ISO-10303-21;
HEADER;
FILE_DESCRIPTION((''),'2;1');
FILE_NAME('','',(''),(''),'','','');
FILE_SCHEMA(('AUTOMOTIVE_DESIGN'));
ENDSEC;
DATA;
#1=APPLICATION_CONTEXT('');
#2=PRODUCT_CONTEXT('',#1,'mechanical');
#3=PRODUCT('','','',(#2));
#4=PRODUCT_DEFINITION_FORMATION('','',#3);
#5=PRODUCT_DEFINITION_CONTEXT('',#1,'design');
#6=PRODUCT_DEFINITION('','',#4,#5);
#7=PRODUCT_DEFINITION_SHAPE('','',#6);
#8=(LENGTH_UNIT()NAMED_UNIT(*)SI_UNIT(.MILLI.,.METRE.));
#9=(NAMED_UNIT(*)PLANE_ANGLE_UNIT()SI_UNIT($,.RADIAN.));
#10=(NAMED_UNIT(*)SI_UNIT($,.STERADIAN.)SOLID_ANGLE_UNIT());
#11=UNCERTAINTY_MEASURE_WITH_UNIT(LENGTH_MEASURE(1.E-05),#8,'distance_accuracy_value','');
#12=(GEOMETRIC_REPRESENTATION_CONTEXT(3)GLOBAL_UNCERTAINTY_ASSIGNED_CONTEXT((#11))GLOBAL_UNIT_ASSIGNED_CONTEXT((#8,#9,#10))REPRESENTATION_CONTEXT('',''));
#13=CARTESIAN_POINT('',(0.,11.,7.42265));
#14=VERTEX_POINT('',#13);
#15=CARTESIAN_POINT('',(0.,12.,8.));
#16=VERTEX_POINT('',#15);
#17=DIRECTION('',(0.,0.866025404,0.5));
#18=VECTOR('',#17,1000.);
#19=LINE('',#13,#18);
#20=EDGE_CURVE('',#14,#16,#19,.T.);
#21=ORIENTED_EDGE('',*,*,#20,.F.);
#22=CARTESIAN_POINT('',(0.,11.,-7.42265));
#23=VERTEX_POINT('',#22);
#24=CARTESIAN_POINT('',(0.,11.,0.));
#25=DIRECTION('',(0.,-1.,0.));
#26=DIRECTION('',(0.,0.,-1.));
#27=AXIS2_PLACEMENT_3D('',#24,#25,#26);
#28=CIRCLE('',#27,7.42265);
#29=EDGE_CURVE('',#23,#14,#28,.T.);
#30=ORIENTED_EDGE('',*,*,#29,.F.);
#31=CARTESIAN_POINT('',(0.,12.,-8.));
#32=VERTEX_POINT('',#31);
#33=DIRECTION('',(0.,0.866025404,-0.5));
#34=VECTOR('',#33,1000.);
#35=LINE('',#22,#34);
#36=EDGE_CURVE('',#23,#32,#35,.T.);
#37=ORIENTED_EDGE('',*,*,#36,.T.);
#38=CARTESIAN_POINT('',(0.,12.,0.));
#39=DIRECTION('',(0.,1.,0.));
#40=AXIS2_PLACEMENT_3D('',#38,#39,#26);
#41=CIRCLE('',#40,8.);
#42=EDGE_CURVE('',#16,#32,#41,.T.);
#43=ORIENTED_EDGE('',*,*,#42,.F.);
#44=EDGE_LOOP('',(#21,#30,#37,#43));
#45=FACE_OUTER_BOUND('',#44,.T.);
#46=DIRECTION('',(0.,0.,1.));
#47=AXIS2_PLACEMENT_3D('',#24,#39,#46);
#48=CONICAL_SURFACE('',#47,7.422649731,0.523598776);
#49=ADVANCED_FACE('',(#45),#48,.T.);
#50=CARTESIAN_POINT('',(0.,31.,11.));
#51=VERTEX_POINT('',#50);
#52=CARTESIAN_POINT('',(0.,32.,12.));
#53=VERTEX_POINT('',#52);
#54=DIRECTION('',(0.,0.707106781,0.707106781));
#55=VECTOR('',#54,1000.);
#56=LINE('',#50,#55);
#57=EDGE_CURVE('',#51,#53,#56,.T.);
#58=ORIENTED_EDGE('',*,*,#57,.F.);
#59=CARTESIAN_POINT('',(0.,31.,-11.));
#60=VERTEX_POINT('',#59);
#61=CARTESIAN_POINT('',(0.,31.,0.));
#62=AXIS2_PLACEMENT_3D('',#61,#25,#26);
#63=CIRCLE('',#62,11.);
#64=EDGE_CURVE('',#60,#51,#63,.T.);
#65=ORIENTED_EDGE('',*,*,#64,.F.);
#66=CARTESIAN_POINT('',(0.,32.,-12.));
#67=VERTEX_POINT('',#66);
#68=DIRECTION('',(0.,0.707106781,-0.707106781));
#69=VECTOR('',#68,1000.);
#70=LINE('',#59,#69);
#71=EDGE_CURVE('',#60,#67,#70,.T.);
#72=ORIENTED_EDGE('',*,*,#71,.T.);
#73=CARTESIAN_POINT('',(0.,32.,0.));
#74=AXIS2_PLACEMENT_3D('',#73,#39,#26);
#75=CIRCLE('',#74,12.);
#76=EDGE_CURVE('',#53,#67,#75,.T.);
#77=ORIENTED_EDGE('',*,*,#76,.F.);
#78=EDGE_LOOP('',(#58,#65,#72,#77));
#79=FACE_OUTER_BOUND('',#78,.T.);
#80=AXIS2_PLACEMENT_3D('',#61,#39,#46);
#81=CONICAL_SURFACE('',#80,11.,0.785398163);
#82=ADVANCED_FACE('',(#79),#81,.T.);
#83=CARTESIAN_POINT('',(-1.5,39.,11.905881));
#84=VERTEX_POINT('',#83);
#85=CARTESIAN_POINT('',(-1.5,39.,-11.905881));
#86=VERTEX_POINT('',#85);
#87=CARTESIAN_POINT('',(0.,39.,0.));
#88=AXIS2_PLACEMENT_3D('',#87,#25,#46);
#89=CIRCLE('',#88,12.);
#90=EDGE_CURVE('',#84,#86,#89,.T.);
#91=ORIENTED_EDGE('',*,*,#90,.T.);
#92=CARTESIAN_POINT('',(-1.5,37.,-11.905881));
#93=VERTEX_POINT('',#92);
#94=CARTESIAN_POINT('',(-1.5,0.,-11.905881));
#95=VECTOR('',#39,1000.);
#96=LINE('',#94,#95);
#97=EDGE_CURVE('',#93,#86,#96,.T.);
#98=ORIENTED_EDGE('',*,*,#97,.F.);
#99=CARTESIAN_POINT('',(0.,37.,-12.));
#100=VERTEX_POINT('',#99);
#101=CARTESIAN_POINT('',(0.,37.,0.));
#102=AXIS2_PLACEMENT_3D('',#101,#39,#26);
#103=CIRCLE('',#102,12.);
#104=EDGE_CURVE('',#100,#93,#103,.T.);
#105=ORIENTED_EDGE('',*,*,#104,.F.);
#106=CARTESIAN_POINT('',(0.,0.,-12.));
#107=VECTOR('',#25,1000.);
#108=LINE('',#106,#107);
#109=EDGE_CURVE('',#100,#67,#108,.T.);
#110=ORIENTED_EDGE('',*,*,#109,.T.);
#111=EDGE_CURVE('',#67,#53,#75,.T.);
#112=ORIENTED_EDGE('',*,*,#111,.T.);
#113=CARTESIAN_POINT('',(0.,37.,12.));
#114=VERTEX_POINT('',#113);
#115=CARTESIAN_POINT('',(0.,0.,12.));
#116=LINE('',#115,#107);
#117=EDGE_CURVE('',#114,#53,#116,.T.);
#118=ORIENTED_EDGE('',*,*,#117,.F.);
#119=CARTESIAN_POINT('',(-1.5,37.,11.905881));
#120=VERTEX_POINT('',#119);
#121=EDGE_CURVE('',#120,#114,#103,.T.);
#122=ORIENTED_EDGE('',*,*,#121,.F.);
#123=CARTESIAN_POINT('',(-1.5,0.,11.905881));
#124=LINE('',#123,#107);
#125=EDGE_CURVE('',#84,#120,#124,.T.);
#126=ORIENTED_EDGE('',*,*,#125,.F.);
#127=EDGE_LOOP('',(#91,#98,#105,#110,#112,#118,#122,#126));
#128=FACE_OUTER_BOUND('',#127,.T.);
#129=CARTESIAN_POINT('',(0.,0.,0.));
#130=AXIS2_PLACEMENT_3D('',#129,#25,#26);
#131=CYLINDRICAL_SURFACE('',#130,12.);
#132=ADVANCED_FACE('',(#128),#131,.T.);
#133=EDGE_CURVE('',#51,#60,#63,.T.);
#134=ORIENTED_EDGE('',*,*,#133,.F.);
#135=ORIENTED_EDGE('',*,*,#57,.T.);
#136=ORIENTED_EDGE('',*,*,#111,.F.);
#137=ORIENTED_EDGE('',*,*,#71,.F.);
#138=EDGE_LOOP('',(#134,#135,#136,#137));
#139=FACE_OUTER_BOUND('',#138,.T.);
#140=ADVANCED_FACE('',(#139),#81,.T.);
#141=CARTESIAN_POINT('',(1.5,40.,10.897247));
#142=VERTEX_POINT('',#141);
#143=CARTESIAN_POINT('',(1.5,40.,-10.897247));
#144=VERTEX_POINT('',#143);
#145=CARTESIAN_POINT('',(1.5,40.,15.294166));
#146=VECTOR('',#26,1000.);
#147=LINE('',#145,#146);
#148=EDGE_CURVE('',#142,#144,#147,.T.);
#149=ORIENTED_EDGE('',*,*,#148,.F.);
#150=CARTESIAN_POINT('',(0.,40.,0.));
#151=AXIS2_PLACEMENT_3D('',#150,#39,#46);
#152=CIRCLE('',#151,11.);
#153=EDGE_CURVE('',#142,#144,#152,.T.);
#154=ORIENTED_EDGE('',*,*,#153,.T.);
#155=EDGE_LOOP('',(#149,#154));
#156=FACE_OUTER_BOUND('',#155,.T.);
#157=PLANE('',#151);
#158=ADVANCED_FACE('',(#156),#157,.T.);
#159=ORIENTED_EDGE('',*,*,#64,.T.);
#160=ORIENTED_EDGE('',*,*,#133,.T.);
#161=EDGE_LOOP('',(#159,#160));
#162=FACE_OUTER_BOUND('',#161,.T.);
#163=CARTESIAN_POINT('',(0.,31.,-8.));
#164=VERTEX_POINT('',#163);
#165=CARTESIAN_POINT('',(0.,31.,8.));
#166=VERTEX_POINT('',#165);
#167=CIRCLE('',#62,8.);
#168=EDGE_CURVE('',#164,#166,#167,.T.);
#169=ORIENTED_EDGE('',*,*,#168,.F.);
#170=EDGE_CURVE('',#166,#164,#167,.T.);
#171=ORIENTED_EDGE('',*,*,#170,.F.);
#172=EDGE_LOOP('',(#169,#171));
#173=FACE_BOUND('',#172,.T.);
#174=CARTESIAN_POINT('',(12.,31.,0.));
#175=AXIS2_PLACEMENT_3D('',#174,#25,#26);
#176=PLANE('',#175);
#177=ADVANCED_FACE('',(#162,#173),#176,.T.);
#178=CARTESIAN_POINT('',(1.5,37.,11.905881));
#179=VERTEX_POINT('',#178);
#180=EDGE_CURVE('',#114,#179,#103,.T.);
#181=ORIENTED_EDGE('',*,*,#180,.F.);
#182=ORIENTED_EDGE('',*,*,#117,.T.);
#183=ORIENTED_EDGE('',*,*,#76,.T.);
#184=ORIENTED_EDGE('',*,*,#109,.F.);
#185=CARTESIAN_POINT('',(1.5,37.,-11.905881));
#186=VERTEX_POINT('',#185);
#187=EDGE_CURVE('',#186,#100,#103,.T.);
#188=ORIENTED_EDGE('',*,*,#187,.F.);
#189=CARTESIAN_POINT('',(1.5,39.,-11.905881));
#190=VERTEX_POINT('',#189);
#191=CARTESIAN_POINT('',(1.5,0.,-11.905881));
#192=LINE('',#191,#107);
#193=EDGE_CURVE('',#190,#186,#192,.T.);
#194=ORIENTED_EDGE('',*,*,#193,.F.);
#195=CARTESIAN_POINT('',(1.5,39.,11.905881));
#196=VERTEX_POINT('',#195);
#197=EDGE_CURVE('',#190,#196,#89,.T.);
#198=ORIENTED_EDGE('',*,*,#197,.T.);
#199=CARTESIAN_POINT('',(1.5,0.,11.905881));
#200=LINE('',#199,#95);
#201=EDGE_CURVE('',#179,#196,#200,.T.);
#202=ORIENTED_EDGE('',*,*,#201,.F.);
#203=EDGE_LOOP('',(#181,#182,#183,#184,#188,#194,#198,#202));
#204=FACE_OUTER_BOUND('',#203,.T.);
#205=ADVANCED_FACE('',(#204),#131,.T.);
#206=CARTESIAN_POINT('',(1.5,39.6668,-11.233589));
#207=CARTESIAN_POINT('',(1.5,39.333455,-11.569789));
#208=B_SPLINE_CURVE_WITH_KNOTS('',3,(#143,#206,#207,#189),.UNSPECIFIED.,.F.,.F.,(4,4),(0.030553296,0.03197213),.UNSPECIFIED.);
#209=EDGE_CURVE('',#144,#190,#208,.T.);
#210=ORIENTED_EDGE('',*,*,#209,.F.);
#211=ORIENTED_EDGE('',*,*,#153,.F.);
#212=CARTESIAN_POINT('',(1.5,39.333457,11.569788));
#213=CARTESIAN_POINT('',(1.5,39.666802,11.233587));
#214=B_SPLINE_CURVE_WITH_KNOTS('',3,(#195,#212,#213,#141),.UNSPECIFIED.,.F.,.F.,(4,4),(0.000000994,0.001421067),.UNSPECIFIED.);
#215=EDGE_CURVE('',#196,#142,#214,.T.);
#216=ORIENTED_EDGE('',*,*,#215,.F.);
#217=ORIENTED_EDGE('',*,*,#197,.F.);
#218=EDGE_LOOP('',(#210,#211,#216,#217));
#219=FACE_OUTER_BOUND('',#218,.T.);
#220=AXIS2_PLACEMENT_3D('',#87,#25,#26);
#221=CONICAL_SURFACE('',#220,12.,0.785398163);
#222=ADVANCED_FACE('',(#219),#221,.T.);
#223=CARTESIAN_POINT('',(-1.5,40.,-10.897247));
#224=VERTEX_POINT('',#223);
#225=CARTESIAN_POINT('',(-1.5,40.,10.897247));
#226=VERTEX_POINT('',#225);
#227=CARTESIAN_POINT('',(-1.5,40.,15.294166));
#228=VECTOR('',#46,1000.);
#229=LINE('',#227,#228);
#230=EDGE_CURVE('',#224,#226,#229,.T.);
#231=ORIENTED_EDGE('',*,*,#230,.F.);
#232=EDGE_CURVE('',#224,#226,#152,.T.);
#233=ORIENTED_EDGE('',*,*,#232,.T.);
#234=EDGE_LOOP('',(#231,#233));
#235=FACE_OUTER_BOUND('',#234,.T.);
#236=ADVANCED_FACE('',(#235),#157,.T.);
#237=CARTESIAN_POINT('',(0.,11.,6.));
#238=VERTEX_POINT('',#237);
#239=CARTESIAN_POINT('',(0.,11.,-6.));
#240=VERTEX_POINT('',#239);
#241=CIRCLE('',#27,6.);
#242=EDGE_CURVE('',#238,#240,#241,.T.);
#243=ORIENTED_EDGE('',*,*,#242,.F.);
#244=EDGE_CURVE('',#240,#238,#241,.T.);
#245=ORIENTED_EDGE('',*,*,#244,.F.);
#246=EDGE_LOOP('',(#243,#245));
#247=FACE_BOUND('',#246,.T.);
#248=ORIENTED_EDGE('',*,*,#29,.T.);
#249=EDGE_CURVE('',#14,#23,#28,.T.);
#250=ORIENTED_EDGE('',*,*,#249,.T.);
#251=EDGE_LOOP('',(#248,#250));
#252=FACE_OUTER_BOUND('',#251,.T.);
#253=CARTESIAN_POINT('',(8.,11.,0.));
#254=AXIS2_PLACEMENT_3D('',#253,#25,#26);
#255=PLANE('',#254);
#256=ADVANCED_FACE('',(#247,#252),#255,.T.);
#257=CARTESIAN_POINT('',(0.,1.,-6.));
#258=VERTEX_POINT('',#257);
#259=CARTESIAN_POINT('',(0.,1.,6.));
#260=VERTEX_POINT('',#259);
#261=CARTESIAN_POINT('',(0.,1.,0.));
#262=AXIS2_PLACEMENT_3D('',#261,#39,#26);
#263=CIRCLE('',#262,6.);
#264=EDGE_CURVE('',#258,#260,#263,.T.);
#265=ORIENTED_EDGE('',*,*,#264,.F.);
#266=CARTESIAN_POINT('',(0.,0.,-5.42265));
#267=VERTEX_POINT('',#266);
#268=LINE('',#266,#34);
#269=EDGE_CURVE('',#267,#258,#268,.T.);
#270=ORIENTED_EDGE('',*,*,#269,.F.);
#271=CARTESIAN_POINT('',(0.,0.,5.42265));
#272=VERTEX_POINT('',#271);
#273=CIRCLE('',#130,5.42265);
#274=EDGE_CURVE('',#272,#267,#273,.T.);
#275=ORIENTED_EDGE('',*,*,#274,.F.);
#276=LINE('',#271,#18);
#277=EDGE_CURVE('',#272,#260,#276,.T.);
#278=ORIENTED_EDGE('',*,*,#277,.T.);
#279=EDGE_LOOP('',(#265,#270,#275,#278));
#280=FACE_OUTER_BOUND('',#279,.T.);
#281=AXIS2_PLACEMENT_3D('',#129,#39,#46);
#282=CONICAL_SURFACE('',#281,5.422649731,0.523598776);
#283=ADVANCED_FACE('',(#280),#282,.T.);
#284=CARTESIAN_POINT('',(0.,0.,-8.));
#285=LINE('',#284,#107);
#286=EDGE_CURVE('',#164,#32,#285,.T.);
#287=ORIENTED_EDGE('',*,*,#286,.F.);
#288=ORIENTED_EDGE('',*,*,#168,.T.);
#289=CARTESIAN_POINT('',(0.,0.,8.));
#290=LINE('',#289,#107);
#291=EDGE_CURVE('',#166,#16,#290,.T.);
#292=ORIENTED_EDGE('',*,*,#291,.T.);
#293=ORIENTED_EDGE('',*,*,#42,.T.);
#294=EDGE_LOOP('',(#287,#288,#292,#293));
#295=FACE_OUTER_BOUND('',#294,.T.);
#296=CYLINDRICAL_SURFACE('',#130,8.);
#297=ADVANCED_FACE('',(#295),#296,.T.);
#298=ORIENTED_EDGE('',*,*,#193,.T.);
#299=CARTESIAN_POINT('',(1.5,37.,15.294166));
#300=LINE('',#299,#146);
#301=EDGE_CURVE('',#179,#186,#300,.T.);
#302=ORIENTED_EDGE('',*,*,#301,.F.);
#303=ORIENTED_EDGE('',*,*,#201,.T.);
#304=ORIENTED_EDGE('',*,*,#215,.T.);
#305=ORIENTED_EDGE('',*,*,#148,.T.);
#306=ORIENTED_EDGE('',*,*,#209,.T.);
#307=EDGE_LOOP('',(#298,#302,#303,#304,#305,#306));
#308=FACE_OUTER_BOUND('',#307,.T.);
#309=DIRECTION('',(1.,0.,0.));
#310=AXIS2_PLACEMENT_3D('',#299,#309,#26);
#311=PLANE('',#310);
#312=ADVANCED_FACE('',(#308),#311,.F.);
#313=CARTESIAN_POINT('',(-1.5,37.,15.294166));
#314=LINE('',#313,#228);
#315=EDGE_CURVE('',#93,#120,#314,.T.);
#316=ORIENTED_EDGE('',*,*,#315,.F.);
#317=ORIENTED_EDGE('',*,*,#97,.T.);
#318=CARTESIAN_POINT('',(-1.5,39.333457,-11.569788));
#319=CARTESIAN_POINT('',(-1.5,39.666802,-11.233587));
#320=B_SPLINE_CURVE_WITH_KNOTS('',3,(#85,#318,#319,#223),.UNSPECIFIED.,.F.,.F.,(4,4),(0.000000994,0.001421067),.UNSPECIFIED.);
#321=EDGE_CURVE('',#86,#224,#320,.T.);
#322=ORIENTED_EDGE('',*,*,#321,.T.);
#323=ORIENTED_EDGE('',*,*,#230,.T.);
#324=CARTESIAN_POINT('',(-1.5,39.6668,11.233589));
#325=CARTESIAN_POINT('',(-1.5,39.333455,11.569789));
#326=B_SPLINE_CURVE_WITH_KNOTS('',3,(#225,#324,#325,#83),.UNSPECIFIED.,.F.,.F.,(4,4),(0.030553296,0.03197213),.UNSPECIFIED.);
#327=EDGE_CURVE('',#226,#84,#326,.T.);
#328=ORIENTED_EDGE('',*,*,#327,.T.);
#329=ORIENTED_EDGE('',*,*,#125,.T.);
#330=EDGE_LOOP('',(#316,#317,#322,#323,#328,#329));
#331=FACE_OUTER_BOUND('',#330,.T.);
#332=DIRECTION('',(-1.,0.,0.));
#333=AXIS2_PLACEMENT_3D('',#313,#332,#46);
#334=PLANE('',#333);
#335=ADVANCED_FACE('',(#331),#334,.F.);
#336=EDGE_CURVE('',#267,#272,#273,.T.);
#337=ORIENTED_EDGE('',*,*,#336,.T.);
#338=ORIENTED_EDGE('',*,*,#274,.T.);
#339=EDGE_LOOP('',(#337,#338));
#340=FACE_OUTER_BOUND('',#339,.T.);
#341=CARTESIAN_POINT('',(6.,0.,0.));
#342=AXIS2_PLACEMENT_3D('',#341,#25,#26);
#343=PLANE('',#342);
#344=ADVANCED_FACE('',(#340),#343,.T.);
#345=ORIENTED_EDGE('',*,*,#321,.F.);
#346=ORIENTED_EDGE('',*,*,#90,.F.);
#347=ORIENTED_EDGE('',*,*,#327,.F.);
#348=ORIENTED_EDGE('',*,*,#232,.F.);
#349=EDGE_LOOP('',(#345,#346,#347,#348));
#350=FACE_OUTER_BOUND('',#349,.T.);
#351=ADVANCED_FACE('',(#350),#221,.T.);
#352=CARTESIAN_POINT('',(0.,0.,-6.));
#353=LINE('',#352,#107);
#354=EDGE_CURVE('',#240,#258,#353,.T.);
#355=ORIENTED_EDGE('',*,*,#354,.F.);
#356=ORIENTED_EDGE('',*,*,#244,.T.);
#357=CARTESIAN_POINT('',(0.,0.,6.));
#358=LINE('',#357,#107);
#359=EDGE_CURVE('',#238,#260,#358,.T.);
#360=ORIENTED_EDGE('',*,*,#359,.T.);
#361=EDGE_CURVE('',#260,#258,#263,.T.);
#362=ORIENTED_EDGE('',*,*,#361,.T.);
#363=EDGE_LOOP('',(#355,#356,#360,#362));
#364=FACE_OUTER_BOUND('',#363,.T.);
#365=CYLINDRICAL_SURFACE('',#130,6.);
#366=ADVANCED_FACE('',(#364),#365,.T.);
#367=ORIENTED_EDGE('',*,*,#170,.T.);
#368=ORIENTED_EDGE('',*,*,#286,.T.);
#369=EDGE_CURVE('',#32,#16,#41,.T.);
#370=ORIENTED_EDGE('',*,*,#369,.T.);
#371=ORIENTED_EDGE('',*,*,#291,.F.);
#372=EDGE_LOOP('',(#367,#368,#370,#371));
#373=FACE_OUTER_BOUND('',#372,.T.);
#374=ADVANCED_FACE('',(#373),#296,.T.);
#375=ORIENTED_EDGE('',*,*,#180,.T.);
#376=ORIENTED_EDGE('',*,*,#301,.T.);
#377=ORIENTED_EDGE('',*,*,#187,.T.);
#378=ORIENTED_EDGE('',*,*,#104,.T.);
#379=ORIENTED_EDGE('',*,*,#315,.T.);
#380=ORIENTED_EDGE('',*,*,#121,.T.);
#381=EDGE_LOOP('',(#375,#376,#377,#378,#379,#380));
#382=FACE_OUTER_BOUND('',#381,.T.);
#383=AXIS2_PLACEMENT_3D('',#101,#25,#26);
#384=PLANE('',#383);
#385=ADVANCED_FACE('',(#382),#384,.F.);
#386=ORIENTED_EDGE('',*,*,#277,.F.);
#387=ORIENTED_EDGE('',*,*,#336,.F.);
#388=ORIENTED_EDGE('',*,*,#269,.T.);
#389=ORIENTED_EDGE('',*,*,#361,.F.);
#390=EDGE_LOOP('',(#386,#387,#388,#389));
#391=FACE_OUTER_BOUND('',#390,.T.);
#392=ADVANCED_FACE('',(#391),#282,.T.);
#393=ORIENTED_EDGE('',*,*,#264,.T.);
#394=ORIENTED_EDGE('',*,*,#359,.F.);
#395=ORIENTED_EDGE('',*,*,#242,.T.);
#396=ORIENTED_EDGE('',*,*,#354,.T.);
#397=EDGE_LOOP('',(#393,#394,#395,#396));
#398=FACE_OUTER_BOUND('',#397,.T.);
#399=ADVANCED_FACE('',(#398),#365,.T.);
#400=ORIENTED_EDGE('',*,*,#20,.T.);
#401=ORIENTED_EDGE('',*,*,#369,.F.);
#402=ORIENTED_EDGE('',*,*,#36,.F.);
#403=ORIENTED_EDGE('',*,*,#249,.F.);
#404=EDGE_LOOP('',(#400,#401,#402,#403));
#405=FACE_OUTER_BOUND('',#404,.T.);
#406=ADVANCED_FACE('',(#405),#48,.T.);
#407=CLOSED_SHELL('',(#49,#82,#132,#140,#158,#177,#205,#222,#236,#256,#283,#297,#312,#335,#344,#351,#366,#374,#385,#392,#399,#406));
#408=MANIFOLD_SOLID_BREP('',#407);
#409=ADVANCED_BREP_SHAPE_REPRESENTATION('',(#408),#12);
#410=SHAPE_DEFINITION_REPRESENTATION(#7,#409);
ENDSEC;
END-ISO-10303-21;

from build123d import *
from OCP.BRepFilletAPI import BRepFilletAPI_MakeChamfer

# Parameters (mm, degrees)
CHAMFER1_SIZE      = 1
CHAMFER2_SIZE      = 1
CHAMFER2_SIZE2     = 0.577350269
SKETCH2_W          = 3
SKETCH2_H          = 30.588331256
CUT_EXTRUDE1_DEPTH = 3


with BuildPart() as part:
    # Sketch1 → Revolve1 (revolve)
    with BuildSketch(Plane.XY, mode=Mode.PRIVATE) as revolve1_sk:
        Polygon((0, 0), (0, 40), (12, 40), (12, 31), (8, 31), (8, 11), (6, 11), (6, 0), align=None)
    revolve(revolve1_sk.sketch.rotate(Axis((0, 0, 0), (0, 1, 0)), 90), axis=Axis((0, 0, 0), (0, 1, 0)))

    # Chamfer1
    chamfer1_edges = [part.edges().sort_by_distance(p)[0] for p in [
        (0, 31, 12),
        (0, 40, 12),
    ]]
    chamfer(chamfer1_edges, length=CHAMFER1_SIZE)

    # Chamfer2: one chamfer whose edges measure the first distance from different faces: ONE call of the kernel's chamfer builder (chamfer() names one face for all edges)
    chamfer2_edges_1 = [part.edges().sort_by_distance(p)[0] for p in [
        (0, 0, 6),
    ]]
    chamfer2_side_1 = [part.faces().sort_by_distance(p)[0] for p in [
        (0, 5.5, 6),
    ]]
    chamfer2_edges_2 = [part.edges().sort_by_distance(p)[0] for p in [
        (0, 11, 8),
    ]]
    chamfer2_side_2 = [part.faces().sort_by_distance(p)[0] for p in [
        (0, 21, 8),
    ]]
    chamfer2 = BRepFilletAPI_MakeChamfer(part.part.solid().wrapped)
    for e in chamfer2_edges_1:
        chamfer2.Add(CHAMFER2_SIZE, CHAMFER2_SIZE2, e.wrapped, chamfer2_side_1[0].wrapped)  # the first distance lies on this face
    for e in chamfer2_edges_2:
        chamfer2.Add(CHAMFER2_SIZE, CHAMFER2_SIZE2, e.wrapped, chamfer2_side_2[0].wrapped)  # the first distance lies on this face
    add(Compound.cast(chamfer2.Shape()), mode=Mode.REPLACE)

    # Sketch2 → Cut-Extrude1 (cut)
    with BuildSketch(Plane(origin=(0, 40, 0), x_dir=(1, 0, 0), z_dir=(0, 1, 0))):
        Rectangle(SKETCH2_W, SKETCH2_H)
    extrude(amount=-CUT_EXTRUDE1_DEPTH, mode=Mode.SUBTRACT)


solid = part.part
